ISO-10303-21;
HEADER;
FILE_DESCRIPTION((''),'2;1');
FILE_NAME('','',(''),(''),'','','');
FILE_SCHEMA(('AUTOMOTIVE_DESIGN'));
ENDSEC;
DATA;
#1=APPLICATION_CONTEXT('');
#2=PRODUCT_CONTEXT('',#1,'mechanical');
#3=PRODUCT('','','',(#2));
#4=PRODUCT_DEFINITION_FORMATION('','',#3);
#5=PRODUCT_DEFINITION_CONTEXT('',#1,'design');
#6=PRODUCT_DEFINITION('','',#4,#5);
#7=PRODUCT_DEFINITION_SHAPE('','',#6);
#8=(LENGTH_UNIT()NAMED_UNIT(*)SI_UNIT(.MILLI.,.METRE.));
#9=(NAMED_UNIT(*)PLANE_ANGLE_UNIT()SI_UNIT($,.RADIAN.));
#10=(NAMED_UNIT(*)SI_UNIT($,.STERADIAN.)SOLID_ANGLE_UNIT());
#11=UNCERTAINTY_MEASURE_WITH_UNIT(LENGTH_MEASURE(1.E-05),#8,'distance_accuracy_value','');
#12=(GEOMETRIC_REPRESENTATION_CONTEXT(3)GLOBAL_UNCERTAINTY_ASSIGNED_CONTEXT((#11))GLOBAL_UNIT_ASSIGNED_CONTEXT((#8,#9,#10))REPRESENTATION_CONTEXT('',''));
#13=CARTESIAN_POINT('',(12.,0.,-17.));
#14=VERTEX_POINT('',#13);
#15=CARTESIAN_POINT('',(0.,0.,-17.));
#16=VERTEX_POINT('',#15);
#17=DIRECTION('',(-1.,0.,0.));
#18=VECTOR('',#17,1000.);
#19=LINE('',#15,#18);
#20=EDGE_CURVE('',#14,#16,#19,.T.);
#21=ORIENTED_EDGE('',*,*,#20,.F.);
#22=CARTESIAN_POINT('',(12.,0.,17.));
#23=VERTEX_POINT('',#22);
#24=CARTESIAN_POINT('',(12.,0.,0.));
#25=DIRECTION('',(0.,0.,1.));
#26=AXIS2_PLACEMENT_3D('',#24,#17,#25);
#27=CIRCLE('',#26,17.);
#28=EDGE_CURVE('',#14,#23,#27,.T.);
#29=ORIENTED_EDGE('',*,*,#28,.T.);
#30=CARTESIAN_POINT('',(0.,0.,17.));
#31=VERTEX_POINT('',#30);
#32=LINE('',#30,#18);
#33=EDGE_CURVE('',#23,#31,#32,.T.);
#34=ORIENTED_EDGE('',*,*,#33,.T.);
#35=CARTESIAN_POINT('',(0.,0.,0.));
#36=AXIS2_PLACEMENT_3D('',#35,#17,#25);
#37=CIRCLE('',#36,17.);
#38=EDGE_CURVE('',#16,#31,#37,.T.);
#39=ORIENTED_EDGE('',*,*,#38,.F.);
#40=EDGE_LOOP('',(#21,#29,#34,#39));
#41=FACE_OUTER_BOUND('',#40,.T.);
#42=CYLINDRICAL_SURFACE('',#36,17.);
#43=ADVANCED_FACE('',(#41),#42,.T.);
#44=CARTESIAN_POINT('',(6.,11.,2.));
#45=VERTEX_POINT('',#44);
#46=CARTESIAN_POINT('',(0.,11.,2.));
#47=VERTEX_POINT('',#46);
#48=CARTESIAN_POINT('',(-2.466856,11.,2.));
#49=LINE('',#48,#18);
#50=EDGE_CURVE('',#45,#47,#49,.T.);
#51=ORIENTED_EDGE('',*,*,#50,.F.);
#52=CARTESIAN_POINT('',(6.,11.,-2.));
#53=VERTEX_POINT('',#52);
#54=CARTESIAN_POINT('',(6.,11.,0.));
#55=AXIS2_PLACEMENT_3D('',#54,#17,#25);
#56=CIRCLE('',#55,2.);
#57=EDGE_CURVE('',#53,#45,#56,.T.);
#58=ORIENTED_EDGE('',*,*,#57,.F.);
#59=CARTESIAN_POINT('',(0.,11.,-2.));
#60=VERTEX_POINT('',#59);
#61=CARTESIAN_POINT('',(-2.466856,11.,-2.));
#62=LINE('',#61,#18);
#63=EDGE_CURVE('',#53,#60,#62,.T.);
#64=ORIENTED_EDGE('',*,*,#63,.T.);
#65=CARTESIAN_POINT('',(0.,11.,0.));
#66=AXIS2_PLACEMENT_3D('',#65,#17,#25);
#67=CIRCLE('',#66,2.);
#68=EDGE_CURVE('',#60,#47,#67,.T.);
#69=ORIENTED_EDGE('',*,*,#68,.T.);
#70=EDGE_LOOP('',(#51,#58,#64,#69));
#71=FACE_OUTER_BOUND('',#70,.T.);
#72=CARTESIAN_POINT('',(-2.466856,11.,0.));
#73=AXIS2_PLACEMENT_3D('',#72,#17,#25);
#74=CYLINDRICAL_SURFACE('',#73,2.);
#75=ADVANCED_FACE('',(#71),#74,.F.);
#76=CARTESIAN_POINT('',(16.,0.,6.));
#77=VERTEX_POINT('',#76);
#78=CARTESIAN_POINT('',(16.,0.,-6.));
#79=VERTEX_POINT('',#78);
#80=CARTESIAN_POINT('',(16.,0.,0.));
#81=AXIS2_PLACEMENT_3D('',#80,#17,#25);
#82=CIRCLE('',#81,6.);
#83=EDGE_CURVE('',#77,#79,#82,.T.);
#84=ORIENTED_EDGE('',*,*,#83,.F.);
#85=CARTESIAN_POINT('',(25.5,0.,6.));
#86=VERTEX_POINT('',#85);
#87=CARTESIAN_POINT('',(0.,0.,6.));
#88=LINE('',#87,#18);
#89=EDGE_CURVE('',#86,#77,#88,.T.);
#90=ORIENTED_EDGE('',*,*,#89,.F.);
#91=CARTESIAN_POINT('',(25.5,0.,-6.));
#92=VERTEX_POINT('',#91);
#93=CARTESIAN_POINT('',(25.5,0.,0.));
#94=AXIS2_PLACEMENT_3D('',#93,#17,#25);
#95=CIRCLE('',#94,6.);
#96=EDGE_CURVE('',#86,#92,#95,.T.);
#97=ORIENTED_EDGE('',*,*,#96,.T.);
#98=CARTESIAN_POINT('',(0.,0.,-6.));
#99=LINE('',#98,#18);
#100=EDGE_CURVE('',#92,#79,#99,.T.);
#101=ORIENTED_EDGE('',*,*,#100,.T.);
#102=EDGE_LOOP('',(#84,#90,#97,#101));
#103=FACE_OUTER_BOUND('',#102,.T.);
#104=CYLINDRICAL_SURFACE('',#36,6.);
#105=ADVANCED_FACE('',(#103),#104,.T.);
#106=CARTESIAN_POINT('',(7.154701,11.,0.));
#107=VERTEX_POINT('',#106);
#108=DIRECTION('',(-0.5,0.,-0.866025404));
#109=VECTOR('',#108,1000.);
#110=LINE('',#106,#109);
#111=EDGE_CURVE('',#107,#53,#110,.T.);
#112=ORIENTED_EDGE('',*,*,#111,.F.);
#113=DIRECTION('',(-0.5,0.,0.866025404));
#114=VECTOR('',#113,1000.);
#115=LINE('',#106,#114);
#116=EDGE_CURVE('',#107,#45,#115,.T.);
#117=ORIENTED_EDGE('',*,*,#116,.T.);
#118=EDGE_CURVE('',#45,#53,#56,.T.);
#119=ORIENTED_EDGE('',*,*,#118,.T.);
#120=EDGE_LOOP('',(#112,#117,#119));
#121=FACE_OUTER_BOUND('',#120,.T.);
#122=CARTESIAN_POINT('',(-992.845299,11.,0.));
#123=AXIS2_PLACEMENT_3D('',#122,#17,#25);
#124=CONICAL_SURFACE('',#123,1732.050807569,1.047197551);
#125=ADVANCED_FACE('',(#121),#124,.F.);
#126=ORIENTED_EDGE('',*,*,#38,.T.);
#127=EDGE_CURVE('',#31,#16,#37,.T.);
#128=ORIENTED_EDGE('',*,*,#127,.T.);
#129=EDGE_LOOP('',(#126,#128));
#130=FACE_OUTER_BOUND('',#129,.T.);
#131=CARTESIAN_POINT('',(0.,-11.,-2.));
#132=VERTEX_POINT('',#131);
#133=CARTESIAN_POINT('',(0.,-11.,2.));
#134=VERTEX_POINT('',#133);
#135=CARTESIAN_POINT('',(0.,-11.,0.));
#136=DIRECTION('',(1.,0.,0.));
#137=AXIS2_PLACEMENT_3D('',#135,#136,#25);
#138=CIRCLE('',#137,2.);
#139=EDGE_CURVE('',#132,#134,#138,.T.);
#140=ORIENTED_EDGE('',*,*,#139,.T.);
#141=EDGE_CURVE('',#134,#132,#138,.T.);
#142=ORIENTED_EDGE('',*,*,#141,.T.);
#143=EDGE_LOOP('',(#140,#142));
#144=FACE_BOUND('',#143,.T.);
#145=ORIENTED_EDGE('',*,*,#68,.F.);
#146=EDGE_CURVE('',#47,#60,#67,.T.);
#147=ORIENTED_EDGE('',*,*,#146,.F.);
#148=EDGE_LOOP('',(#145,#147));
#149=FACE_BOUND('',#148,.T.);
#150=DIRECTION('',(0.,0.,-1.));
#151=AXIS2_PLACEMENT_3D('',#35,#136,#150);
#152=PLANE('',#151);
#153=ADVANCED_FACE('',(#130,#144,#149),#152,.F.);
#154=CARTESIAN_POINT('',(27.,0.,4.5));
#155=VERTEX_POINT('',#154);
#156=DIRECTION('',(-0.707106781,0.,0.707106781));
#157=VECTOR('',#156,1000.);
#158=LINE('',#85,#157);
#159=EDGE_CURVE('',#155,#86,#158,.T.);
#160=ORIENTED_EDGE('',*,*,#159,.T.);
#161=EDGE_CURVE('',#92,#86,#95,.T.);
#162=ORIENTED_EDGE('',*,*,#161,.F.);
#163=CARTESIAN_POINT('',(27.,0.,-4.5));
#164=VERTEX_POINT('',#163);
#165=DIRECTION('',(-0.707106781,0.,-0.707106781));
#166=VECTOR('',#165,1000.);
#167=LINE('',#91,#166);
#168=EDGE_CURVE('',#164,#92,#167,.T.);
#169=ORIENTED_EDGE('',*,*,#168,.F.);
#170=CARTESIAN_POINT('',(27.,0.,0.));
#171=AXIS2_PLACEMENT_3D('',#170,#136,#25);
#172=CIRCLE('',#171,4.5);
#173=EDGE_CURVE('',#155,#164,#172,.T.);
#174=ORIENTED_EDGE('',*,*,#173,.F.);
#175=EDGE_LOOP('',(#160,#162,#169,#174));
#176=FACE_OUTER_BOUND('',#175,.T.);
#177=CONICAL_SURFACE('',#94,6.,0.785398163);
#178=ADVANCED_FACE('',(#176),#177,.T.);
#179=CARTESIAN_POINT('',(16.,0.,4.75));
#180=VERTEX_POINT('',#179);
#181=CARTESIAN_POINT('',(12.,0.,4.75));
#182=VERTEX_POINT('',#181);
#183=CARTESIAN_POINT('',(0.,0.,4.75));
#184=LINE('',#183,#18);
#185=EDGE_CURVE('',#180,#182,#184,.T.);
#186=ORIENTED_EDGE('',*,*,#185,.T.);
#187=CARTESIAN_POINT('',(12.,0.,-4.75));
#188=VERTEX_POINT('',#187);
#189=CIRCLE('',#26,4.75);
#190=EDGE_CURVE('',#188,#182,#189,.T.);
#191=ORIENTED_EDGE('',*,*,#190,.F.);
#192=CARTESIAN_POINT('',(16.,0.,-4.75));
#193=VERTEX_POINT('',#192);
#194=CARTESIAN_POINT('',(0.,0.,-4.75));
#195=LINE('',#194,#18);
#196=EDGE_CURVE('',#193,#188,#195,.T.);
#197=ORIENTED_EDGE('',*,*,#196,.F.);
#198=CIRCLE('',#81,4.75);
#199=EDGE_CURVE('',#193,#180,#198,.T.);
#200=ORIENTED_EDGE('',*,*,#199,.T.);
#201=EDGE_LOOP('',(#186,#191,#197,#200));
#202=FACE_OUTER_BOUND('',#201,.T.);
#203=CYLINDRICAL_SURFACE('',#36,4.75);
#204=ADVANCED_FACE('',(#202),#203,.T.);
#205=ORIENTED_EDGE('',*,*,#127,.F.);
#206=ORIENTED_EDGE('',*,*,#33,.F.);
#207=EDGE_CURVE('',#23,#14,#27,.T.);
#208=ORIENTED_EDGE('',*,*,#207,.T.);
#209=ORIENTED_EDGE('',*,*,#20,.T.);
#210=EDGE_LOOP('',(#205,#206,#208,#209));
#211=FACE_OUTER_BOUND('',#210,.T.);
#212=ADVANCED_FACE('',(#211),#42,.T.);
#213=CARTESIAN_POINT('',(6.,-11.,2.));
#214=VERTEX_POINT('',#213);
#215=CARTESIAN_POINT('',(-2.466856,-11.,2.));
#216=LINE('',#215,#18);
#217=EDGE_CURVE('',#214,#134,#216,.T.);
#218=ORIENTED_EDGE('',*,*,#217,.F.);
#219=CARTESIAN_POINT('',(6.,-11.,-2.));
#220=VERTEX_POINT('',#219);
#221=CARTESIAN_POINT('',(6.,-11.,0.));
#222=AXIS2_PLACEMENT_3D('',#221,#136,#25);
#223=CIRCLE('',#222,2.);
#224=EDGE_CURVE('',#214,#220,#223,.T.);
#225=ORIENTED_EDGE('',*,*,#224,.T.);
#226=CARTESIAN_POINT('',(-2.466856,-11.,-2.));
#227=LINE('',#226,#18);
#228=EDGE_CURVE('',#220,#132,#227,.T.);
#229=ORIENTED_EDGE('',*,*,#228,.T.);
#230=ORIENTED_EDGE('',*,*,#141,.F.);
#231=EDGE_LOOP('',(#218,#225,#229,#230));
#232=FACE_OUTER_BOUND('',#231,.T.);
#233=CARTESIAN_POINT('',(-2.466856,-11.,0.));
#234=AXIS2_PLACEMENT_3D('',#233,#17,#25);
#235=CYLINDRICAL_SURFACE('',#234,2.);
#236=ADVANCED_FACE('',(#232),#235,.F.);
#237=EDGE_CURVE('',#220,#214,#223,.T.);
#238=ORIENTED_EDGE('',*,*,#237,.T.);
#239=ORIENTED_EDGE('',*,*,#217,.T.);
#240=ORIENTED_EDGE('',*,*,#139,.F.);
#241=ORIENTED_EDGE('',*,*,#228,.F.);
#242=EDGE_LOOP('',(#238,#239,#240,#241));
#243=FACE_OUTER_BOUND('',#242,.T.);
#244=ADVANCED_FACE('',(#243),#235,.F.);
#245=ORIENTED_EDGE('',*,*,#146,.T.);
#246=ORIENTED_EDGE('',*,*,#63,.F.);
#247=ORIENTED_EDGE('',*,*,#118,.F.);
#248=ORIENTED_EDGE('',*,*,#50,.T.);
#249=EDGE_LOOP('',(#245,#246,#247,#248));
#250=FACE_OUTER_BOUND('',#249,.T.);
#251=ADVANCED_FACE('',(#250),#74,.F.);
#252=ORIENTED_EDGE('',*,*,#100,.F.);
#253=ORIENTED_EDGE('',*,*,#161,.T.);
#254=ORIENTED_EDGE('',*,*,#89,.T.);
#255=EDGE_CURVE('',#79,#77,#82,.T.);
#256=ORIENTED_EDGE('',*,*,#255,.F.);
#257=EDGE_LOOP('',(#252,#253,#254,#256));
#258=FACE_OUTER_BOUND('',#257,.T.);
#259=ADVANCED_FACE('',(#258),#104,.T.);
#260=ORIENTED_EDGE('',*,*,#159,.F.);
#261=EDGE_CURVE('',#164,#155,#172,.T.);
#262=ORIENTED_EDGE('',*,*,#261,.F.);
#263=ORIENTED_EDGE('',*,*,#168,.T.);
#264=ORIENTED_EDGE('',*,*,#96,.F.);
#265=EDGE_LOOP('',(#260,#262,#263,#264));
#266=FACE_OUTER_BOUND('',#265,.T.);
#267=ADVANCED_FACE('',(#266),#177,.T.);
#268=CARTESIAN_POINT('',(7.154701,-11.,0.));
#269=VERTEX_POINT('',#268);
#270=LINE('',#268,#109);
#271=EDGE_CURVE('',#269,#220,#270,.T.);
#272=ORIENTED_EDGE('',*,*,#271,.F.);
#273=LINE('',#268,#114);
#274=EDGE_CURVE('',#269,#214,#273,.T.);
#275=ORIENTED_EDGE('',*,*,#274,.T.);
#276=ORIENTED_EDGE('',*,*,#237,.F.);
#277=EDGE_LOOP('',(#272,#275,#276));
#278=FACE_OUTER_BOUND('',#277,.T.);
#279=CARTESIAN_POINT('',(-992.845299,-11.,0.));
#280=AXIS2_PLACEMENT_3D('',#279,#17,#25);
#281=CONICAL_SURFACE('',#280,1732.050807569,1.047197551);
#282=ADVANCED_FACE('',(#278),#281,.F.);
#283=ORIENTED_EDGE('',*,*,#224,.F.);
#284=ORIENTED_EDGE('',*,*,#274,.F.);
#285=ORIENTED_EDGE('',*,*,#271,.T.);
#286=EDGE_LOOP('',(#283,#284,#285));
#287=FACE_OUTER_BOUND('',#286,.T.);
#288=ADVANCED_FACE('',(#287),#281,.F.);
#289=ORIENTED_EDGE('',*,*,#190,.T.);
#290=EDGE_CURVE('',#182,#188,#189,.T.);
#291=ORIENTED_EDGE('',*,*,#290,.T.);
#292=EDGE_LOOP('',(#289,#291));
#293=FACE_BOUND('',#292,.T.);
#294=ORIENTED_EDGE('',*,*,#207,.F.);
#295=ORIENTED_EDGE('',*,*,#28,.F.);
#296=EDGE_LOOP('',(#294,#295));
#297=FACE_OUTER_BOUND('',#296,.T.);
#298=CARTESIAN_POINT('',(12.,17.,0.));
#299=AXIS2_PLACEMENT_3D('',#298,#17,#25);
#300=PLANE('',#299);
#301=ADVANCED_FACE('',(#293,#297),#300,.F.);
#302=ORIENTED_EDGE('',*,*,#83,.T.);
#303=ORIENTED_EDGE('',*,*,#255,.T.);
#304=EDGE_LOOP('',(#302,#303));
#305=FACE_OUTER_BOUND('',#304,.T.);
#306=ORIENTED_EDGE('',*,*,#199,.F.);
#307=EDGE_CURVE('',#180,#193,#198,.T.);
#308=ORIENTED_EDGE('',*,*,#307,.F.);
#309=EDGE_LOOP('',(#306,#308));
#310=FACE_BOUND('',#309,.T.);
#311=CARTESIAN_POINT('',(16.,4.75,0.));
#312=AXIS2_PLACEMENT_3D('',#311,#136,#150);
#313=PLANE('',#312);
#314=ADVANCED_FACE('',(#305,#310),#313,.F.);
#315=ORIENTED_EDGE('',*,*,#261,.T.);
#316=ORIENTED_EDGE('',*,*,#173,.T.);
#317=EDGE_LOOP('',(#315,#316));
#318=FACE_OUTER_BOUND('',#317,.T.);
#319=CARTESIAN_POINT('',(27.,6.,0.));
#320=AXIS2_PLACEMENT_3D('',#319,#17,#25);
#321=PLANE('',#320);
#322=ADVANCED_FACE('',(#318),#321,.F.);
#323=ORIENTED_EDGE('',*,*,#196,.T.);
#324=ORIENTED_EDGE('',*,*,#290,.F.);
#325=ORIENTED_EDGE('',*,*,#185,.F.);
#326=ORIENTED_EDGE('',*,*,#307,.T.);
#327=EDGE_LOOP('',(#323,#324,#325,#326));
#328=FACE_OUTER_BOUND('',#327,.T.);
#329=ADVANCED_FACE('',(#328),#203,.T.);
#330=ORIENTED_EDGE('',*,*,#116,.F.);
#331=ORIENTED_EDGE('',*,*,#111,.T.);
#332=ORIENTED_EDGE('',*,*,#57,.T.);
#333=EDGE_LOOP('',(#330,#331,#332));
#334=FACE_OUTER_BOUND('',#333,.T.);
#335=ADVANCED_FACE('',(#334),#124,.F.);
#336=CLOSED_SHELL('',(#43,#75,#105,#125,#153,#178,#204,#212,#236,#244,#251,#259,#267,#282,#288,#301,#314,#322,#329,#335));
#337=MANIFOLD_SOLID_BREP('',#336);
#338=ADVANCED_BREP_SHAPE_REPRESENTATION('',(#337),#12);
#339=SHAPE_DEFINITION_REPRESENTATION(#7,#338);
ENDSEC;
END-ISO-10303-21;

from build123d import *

# Parameters (mm, degrees)
CHAMFER1_SIZE = 1.5


with BuildPart() as part:
    # Sketch1 → Revolve1 (revolve)
    with BuildSketch(Plane.XY, mode=Mode.PRIVATE) as revolve1_sk:
        Polygon((0, 0), (0, 17), (12, 17), (12, 4.75), (16, 4.75), (16, 6), (27, 6), (27, 0), align=None)
    revolve(revolve1_sk.sketch.rotate(Axis((0, 0, 0), (1, 0, 0)), 90), axis=Axis((0, 0, 0), (1, 0, 0)))

    # Chamfer1
    chamfer1_edges = [part.edges().sort_by_distance(p)[0] for p in [
        (27, 0, -6),
    ]]
    chamfer(chamfer1_edges, length=CHAMFER1_SIZE)

    # Sketch2 → Cut-Revolve1 (revolve, cut)
    with BuildSketch(Plane.XY, mode=Mode.PRIVATE) as cut_revolve1_sk:
        Polygon((0, 11), (0, 13), (6, 13), (7.154700538, 11), align=None)
    cut_revolve1 = revolve(cut_revolve1_sk.sketch.rotate(Axis((-2.466856423, 11, 0), (1, 0, 0)), 90), axis=Axis((-2.466856423, 11, 0), (1, 0, 0)), mode=Mode.SUBTRACT)

    # Mirror1: Cut-Revolve1 across plane
    add(cut_revolve1.mirror(Plane.ZX), mode=Mode.SUBTRACT)


solid = part.part
